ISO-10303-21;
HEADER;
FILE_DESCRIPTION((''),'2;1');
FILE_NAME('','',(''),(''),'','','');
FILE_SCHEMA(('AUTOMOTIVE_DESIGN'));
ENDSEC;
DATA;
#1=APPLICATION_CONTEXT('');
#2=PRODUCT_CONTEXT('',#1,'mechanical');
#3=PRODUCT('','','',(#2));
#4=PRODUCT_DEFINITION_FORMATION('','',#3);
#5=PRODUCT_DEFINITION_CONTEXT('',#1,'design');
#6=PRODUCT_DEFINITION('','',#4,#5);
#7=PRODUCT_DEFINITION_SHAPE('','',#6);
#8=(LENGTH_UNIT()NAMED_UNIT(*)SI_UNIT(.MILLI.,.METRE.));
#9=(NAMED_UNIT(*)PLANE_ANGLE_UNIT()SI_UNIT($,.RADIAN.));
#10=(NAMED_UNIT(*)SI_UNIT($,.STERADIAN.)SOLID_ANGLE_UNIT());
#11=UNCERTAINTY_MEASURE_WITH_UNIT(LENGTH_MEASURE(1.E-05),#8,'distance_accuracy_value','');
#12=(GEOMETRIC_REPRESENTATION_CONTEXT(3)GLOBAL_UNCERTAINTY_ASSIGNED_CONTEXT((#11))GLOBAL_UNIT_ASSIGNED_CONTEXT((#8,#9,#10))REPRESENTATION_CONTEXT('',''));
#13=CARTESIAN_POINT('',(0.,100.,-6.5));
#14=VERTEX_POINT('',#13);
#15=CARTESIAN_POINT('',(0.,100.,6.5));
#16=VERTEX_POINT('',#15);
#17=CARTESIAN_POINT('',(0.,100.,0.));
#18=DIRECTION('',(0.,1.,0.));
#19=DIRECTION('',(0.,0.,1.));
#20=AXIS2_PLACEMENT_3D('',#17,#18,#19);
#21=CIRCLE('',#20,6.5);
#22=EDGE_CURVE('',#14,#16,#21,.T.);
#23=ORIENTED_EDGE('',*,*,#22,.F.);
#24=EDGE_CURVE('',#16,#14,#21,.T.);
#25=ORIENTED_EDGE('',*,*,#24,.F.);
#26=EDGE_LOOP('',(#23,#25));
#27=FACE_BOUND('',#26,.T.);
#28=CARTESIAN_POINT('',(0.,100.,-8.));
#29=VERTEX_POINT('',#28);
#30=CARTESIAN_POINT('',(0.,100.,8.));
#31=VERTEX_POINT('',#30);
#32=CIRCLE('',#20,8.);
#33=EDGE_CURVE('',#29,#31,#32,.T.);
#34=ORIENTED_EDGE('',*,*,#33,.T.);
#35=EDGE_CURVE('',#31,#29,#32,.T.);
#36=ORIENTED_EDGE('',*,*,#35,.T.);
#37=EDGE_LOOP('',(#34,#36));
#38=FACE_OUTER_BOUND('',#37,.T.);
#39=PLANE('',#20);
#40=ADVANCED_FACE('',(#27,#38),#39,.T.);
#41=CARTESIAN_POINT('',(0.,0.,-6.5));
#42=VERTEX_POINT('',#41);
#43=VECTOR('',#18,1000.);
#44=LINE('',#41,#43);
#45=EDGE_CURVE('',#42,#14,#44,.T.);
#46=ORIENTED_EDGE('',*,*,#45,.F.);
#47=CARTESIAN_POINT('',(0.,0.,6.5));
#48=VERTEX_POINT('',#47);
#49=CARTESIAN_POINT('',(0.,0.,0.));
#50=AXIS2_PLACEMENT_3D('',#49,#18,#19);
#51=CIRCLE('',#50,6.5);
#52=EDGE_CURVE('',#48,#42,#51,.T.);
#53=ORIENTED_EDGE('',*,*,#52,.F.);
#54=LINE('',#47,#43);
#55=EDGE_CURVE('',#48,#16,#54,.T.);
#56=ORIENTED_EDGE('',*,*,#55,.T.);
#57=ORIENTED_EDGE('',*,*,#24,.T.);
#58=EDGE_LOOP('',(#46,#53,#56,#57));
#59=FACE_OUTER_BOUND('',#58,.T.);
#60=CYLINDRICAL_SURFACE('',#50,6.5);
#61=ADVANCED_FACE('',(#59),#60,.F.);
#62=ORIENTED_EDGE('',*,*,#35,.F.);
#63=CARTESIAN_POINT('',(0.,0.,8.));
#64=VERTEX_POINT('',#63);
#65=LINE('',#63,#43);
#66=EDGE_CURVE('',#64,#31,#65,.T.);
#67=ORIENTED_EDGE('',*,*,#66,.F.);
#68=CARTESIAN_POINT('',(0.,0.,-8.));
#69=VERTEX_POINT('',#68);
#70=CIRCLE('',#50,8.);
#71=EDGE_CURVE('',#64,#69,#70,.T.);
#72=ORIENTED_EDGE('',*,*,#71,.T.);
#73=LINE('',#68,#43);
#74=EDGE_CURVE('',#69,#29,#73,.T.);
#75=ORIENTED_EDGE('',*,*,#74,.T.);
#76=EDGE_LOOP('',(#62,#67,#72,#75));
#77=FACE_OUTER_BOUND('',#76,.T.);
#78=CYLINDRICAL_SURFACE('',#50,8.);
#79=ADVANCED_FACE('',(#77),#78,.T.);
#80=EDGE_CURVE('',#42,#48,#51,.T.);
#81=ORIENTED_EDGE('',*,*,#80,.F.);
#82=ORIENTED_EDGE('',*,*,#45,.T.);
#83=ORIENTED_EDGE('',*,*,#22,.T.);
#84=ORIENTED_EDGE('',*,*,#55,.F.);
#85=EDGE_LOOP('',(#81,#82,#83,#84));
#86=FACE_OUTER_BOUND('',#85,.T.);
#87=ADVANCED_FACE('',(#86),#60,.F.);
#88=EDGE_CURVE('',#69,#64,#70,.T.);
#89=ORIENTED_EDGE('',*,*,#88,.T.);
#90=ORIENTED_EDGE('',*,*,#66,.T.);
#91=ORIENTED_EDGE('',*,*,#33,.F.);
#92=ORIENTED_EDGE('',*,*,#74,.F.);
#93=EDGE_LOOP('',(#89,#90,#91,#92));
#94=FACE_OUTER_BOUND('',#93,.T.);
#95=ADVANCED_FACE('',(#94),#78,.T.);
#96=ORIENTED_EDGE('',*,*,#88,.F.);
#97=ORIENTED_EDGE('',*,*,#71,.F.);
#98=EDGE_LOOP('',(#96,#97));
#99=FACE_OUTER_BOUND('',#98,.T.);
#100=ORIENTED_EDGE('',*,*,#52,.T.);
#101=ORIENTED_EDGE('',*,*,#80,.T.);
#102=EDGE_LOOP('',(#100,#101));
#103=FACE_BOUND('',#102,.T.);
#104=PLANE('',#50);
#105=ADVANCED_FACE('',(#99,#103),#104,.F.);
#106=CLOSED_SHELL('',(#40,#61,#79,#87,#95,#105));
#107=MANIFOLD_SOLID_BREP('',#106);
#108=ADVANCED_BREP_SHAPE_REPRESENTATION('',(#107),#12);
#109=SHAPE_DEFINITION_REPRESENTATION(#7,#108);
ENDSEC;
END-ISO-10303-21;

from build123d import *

# Parameters (mm, degrees)
SWEEP_THIN_PART1_PROFILE_R   = 8
SWEEP_THIN_PART1_PROFILE_R_2 = 6.5


with BuildPart() as part:
    # Sweep-Thin Part1: sweep along a path in Sketch1
    with BuildLine(Plane.XY) as sweep_thin_part1_path:
        Line((0, 0), (0, 100))
    # Sweep-Thin Part1 profile (on start of the path) → Sweep-Thin Part1 (sweep)
    with BuildSketch(Plane.ZX):
        Circle(SWEEP_THIN_PART1_PROFILE_R)
        Circle(SWEEP_THIN_PART1_PROFILE_R_2, mode=Mode.SUBTRACT)
    sweep(path=sweep_thin_part1_path.line)


solid = part.part
